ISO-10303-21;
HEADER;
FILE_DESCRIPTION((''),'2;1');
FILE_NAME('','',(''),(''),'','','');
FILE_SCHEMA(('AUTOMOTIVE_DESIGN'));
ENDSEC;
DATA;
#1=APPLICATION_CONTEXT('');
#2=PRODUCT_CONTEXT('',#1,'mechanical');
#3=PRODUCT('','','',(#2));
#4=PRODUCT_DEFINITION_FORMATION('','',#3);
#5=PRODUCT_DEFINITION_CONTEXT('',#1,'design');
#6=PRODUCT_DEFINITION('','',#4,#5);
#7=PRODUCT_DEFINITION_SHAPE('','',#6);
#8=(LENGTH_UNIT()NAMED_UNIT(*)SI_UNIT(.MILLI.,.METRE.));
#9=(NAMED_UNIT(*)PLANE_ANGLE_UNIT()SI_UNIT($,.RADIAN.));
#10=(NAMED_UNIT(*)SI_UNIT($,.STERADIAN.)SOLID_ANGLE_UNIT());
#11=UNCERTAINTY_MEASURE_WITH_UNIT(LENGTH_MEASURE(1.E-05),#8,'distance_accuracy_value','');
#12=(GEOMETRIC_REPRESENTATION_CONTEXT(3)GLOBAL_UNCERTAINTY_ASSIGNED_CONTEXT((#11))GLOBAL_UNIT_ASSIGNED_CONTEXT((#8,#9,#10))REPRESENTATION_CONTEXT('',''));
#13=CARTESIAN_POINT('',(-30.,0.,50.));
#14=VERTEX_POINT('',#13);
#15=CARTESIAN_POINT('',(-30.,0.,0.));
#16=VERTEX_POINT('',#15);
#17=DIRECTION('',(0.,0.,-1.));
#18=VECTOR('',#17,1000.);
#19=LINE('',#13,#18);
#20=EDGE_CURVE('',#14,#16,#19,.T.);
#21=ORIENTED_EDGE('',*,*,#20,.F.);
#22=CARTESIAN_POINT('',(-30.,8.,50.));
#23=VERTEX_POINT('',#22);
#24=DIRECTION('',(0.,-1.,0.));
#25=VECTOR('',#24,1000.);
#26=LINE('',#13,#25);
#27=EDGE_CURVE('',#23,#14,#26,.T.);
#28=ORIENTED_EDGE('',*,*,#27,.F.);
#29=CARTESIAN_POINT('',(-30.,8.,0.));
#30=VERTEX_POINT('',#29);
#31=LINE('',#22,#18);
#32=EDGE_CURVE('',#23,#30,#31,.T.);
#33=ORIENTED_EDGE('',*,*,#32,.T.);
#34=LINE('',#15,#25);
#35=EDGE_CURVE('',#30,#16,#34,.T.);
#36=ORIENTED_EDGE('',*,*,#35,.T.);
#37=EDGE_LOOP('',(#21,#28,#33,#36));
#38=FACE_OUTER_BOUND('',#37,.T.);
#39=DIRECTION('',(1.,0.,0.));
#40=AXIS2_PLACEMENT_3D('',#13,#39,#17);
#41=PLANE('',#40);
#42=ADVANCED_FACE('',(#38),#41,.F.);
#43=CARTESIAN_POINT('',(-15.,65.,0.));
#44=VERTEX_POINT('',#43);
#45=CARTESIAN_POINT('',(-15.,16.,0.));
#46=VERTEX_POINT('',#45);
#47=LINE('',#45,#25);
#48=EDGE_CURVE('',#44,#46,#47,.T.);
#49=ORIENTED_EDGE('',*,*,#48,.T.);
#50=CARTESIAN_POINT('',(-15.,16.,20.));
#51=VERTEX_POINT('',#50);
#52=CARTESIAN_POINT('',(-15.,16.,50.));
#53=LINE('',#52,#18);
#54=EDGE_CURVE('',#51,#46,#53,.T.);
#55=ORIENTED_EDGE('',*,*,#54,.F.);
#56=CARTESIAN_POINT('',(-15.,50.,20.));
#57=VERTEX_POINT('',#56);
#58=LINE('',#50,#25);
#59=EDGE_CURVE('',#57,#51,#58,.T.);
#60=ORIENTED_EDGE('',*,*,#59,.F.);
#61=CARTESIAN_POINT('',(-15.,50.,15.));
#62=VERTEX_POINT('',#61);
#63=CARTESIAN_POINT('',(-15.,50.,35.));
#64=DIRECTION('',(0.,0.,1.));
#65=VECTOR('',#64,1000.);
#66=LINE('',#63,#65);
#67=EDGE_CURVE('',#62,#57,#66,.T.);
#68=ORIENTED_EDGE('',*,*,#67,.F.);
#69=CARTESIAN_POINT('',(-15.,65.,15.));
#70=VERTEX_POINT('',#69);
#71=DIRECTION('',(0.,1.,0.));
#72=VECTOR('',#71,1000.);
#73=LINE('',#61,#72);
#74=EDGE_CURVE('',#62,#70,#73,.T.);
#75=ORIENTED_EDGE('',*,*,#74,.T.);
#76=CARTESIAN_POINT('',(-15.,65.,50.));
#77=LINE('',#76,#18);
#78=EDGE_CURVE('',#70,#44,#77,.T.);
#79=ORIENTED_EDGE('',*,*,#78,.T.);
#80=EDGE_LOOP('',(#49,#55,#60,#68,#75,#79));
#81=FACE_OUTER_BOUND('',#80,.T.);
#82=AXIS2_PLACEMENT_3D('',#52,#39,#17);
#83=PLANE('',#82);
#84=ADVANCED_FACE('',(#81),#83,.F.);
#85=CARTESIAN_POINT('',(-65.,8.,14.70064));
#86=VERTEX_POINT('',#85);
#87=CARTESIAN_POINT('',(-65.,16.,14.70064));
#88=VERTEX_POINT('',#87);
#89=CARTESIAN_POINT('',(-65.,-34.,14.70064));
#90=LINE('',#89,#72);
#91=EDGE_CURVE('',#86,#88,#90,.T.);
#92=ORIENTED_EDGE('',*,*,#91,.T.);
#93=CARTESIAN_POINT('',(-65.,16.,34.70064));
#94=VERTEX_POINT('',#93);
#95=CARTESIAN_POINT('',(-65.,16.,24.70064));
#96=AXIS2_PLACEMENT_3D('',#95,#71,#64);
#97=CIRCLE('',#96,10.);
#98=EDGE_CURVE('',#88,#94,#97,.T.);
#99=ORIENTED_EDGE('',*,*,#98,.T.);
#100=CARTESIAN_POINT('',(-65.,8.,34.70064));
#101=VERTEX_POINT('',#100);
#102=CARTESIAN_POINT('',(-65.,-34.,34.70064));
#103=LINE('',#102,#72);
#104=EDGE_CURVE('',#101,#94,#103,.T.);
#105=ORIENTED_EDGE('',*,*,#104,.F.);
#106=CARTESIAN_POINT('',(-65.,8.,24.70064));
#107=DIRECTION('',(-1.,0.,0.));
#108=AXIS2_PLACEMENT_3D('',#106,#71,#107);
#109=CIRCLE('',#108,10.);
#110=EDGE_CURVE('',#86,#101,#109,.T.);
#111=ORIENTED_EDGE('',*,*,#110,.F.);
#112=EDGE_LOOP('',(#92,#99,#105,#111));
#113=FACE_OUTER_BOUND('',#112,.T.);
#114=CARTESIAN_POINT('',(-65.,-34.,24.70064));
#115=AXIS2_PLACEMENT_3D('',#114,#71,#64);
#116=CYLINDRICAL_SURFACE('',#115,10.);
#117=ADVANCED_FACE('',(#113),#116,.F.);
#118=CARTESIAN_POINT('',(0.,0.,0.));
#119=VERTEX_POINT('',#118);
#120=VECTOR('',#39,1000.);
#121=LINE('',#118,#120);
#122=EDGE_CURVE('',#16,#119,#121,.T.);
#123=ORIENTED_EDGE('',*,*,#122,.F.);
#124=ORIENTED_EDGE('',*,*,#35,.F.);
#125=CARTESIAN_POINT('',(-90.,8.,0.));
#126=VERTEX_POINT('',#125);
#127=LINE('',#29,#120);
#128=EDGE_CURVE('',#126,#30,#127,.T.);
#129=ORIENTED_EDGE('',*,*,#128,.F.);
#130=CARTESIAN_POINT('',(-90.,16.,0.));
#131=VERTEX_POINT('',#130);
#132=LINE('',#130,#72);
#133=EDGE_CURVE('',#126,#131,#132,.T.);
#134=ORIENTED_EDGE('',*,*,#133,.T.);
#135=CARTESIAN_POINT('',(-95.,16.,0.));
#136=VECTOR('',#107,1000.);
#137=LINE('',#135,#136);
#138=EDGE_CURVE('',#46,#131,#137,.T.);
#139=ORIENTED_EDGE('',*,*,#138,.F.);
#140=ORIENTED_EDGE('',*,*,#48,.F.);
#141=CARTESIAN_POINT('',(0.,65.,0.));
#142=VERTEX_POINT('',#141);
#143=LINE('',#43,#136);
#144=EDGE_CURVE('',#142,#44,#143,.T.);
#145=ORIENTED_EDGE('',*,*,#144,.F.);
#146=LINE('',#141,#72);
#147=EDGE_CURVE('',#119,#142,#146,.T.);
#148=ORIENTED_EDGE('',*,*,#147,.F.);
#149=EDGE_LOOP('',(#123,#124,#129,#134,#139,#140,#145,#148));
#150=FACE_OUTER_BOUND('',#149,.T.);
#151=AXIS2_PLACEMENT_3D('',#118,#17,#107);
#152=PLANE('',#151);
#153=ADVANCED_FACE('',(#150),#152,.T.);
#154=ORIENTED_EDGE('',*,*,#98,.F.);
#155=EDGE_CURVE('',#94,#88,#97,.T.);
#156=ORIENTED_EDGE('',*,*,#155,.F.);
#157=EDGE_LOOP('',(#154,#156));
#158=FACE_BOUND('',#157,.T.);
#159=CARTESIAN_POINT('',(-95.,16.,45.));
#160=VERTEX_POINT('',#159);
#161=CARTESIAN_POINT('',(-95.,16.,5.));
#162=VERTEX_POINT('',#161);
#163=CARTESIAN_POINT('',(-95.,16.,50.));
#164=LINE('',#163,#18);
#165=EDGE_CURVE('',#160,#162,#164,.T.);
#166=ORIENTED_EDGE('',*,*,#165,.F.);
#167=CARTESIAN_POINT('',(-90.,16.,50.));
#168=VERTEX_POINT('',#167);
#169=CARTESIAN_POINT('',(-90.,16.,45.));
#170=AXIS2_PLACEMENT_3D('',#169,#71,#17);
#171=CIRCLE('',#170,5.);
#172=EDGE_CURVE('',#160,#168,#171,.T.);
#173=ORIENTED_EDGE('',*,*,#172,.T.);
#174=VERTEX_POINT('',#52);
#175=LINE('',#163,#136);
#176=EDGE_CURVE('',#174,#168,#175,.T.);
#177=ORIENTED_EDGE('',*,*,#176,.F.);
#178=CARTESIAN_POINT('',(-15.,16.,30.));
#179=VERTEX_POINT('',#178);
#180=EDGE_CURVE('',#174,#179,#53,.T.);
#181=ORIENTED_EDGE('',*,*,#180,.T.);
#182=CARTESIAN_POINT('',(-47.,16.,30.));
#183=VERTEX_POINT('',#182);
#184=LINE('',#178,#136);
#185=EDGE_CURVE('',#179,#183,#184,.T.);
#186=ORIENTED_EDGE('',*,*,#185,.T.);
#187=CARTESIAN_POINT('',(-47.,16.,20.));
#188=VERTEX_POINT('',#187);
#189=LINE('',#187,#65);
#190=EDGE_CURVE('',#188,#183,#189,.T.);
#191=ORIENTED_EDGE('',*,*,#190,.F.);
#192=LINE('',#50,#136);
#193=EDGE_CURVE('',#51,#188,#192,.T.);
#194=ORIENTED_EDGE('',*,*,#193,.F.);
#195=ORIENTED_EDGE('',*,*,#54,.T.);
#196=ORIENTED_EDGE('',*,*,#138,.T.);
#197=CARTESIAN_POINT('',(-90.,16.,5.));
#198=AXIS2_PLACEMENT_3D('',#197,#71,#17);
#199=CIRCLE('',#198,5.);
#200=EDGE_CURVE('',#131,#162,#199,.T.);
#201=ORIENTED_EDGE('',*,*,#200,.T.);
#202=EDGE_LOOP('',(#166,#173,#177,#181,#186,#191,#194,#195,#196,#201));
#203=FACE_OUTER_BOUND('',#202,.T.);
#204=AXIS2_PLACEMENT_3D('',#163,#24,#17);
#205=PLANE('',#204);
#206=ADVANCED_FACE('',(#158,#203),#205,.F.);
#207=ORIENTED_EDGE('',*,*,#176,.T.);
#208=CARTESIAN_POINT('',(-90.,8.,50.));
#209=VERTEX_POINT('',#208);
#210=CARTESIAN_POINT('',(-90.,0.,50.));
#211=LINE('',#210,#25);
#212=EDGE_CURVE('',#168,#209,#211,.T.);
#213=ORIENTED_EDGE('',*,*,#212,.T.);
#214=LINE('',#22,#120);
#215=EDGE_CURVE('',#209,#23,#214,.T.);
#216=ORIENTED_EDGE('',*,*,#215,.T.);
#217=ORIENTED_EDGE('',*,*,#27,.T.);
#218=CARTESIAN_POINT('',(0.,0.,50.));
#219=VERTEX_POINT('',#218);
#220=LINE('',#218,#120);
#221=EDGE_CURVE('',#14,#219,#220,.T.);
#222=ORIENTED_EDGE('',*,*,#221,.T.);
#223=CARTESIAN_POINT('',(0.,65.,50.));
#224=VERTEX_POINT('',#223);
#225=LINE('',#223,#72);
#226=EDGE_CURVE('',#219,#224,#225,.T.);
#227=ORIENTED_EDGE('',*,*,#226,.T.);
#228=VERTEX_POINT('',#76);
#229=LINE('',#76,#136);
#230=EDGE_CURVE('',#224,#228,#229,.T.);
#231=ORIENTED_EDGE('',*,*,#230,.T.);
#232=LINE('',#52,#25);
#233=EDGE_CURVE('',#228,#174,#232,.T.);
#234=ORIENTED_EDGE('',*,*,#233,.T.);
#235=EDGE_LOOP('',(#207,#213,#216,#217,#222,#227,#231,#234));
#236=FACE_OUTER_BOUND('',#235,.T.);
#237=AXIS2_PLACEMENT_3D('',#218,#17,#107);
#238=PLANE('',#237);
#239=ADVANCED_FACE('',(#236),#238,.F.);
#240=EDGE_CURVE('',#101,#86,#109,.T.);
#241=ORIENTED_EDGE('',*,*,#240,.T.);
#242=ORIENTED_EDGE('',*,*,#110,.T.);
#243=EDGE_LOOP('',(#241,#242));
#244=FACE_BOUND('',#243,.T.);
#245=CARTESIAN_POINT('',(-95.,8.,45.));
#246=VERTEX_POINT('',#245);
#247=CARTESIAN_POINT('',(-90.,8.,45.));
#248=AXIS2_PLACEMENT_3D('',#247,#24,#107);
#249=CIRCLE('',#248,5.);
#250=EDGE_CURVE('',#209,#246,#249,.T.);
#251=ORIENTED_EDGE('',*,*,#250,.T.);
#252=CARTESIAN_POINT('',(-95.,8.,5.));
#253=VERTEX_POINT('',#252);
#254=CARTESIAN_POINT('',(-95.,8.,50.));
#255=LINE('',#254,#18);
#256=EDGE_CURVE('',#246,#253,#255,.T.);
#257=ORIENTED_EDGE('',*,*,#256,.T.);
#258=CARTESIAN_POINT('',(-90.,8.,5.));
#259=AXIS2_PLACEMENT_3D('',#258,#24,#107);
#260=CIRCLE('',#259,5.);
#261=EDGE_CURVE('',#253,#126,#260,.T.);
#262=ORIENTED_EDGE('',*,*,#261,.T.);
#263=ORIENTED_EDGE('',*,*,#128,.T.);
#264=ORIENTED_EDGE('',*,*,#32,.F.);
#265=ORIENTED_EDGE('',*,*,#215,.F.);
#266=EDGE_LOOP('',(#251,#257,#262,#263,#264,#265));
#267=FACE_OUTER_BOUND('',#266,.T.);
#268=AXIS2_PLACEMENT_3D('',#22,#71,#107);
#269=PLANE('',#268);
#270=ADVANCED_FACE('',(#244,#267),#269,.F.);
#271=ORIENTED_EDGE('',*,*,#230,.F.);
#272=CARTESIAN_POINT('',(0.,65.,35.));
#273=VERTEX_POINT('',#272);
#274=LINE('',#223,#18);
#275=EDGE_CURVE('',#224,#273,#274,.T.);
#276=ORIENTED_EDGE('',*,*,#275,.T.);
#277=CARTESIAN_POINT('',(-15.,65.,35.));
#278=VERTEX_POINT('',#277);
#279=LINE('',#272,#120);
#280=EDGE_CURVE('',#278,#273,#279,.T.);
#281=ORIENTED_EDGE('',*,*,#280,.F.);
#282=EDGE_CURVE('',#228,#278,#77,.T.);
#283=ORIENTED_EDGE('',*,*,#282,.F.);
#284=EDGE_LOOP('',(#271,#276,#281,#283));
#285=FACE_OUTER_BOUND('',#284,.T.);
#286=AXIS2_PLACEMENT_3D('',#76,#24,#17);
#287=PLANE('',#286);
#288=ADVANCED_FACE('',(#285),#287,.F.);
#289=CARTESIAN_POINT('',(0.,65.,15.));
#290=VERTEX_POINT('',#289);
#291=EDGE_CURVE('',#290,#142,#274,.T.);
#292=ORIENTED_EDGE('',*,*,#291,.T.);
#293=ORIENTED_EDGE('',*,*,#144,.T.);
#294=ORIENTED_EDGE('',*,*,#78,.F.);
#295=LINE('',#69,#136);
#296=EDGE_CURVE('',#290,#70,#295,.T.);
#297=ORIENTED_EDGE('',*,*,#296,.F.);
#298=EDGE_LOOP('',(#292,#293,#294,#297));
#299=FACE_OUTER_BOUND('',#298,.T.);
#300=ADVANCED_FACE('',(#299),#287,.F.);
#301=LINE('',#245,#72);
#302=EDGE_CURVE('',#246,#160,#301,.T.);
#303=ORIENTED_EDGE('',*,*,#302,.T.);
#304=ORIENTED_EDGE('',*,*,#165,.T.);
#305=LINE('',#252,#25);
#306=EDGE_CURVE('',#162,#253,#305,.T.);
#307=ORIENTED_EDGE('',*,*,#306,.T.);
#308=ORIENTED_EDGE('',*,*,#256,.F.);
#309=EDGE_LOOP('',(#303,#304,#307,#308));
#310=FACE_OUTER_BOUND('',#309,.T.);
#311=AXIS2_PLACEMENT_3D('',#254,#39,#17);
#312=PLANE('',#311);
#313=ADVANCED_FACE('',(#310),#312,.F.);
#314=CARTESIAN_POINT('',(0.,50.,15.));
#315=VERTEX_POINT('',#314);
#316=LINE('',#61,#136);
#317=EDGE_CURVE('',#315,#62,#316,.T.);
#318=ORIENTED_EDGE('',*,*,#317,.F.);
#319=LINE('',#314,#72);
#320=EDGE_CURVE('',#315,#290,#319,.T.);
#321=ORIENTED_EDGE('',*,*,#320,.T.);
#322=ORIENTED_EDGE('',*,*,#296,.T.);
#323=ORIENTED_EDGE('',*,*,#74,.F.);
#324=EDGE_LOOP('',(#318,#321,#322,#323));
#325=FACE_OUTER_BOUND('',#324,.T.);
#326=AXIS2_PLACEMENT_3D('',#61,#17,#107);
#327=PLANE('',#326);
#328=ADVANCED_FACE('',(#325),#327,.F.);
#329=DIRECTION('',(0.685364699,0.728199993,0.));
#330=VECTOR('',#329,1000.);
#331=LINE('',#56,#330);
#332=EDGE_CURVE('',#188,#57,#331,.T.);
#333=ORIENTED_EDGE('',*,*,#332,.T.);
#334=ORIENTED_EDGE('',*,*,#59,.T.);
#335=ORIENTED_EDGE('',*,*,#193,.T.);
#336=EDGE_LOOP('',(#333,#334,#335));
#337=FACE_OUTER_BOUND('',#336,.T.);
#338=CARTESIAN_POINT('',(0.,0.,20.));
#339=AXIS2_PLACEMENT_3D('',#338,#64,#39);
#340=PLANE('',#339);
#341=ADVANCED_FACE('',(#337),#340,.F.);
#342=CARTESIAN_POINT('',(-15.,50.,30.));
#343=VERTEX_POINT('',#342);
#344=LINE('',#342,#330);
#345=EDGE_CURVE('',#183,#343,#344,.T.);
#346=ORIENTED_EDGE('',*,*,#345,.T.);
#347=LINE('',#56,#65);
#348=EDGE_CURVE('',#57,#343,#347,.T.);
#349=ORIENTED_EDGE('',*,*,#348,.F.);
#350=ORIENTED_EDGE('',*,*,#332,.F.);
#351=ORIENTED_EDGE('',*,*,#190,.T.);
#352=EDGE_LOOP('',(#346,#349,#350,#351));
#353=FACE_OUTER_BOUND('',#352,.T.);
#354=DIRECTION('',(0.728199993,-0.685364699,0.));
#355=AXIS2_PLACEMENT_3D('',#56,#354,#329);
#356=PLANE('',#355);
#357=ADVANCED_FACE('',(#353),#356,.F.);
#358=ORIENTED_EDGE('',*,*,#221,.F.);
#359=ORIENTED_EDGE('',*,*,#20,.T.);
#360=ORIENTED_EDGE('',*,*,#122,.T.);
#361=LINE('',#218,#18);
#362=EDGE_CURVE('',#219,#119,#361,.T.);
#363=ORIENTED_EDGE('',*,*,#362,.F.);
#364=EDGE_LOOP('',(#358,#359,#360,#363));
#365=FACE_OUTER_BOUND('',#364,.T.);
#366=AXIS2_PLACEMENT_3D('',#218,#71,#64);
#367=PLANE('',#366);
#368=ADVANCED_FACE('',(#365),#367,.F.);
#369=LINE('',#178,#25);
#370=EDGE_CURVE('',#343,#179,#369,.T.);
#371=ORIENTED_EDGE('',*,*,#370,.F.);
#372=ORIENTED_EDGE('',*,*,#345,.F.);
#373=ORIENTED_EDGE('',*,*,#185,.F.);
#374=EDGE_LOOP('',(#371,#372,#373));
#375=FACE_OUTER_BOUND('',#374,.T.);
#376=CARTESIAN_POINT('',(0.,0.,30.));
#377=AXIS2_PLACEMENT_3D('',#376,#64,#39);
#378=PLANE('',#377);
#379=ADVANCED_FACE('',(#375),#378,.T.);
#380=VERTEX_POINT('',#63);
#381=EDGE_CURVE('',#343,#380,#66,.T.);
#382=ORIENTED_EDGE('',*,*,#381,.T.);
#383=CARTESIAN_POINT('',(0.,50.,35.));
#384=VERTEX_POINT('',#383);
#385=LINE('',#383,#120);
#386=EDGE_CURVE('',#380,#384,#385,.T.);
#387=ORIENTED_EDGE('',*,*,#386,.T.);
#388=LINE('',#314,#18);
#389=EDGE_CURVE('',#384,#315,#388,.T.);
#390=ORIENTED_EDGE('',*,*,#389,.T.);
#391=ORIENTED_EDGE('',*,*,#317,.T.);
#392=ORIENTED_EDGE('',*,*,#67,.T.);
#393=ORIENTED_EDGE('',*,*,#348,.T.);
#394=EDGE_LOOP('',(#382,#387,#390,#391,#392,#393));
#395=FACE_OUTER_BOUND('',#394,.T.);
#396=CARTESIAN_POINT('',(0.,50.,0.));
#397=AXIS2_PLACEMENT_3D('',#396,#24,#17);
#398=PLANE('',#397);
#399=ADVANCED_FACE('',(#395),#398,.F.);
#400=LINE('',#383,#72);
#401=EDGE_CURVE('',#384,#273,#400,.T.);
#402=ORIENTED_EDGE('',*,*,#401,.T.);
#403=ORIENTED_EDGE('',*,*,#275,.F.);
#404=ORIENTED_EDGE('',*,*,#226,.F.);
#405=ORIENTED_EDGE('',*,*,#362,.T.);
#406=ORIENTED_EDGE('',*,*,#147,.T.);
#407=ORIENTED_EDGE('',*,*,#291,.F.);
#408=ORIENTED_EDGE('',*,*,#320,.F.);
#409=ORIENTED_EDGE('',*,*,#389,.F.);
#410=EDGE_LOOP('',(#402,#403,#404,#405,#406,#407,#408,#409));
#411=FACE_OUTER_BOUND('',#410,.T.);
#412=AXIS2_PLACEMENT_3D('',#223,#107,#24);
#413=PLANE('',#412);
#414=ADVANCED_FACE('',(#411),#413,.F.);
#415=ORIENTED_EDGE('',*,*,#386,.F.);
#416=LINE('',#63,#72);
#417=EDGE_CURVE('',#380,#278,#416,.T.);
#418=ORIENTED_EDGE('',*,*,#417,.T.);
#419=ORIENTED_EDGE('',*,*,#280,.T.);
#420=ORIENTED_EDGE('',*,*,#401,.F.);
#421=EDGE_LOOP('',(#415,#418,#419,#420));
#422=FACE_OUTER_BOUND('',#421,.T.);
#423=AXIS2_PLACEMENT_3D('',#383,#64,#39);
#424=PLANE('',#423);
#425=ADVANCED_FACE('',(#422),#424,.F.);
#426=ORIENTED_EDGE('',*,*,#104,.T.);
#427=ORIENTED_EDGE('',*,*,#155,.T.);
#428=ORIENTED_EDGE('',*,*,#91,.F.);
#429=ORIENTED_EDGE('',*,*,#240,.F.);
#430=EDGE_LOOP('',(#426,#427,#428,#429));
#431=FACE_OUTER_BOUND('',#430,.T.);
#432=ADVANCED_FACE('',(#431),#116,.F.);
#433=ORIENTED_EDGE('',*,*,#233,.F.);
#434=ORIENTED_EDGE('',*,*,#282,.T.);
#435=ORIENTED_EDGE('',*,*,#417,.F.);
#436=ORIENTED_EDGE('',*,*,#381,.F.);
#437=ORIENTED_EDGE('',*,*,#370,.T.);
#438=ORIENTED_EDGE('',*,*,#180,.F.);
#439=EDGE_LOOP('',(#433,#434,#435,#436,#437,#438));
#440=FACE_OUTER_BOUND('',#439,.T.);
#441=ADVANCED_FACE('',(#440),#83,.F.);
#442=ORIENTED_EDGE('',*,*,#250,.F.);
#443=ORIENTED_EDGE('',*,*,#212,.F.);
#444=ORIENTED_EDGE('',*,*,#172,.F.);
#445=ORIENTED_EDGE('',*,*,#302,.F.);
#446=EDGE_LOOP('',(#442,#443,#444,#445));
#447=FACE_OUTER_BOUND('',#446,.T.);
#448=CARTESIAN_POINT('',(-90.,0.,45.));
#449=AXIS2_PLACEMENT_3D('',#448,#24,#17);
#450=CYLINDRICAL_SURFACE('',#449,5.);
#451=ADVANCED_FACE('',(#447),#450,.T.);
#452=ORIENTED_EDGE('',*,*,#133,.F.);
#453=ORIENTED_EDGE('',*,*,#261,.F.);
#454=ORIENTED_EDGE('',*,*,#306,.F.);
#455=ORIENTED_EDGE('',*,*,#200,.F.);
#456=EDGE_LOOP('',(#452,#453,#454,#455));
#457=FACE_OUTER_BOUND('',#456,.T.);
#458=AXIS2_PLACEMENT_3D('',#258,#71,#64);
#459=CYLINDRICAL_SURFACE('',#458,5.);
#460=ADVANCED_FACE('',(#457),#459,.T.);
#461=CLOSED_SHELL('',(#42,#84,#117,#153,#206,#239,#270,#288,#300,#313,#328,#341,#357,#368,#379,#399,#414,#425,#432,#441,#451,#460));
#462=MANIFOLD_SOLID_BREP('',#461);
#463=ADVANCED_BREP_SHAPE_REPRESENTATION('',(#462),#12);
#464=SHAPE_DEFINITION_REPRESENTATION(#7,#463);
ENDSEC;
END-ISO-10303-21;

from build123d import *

# Parameters (mm, degrees)
BRACKET_BODY_DEPTH        = 50
THROUGH_HOLE_SKETCH_R     = 10
THROUGH_HOLE_DEPTH        = 50
UPRIGHT_NOTCH_20X10_DEPTH = 15
CORNER_FILLET_R5_R        = 5
SIDE_TAB_DEPTH            = 5


with BuildPart() as part:
    # Bracket L-Profile Sketch → Bracket Body (new body)
    with BuildSketch(Plane.XY):
        Polygon((0, 65), (0, 0), (-30, 0), (-30, 8), (-95, 8), (-95, 16), (-15, 16), (-15, 65), align=None)
    extrude(amount=BRACKET_BODY_DEPTH)

    # Through Hole Sketch → Through Hole (cut)
    with BuildSketch(Plane(origin=(0, 16, 0), x_dir=(1, 0, 0), z_dir=(0, 1, 0))):
        with Locations(Location((-65, -24.700639753, 0), (0, 0, 270))):
            Circle(THROUGH_HOLE_SKETCH_R)
    extrude(amount=-THROUGH_HOLE_DEPTH, mode=Mode.SUBTRACT)

    # Upright Notch Sketch → Upright Notch 20x10 (cut)
    with BuildSketch(Plane(origin=(0, 65, 0), x_dir=(1, 0, 0), z_dir=(0, 1, 0))):
        Polygon((0, -25), (0, -35), (-15, -35), (-15, -15), (0, -15), align=None)
    extrude(amount=-UPRIGHT_NOTCH_20X10_DEPTH, mode=Mode.SUBTRACT)

    # Corner Fillet R5
    corner_fillet_r5_edges = [part.edges().sort_by_distance(p)[0] for p in [
        (-95, 12, 0),
        (-95, 12, 50),
    ]]
    fillet(corner_fillet_r5_edges, radius=CORNER_FILLET_R5_R)

    # Side Tab Sketch → Side Tab (add, symmetric)
    with BuildSketch(Plane(origin=(0, 0, 25), x_dir=(-1, 0, 0), z_dir=(0, 0, -1))):
        Polygon((15, 16), (47, 16), (15, 50), align=None)
    extrude(amount=SIDE_TAB_DEPTH, both=True)


solid = part.part
